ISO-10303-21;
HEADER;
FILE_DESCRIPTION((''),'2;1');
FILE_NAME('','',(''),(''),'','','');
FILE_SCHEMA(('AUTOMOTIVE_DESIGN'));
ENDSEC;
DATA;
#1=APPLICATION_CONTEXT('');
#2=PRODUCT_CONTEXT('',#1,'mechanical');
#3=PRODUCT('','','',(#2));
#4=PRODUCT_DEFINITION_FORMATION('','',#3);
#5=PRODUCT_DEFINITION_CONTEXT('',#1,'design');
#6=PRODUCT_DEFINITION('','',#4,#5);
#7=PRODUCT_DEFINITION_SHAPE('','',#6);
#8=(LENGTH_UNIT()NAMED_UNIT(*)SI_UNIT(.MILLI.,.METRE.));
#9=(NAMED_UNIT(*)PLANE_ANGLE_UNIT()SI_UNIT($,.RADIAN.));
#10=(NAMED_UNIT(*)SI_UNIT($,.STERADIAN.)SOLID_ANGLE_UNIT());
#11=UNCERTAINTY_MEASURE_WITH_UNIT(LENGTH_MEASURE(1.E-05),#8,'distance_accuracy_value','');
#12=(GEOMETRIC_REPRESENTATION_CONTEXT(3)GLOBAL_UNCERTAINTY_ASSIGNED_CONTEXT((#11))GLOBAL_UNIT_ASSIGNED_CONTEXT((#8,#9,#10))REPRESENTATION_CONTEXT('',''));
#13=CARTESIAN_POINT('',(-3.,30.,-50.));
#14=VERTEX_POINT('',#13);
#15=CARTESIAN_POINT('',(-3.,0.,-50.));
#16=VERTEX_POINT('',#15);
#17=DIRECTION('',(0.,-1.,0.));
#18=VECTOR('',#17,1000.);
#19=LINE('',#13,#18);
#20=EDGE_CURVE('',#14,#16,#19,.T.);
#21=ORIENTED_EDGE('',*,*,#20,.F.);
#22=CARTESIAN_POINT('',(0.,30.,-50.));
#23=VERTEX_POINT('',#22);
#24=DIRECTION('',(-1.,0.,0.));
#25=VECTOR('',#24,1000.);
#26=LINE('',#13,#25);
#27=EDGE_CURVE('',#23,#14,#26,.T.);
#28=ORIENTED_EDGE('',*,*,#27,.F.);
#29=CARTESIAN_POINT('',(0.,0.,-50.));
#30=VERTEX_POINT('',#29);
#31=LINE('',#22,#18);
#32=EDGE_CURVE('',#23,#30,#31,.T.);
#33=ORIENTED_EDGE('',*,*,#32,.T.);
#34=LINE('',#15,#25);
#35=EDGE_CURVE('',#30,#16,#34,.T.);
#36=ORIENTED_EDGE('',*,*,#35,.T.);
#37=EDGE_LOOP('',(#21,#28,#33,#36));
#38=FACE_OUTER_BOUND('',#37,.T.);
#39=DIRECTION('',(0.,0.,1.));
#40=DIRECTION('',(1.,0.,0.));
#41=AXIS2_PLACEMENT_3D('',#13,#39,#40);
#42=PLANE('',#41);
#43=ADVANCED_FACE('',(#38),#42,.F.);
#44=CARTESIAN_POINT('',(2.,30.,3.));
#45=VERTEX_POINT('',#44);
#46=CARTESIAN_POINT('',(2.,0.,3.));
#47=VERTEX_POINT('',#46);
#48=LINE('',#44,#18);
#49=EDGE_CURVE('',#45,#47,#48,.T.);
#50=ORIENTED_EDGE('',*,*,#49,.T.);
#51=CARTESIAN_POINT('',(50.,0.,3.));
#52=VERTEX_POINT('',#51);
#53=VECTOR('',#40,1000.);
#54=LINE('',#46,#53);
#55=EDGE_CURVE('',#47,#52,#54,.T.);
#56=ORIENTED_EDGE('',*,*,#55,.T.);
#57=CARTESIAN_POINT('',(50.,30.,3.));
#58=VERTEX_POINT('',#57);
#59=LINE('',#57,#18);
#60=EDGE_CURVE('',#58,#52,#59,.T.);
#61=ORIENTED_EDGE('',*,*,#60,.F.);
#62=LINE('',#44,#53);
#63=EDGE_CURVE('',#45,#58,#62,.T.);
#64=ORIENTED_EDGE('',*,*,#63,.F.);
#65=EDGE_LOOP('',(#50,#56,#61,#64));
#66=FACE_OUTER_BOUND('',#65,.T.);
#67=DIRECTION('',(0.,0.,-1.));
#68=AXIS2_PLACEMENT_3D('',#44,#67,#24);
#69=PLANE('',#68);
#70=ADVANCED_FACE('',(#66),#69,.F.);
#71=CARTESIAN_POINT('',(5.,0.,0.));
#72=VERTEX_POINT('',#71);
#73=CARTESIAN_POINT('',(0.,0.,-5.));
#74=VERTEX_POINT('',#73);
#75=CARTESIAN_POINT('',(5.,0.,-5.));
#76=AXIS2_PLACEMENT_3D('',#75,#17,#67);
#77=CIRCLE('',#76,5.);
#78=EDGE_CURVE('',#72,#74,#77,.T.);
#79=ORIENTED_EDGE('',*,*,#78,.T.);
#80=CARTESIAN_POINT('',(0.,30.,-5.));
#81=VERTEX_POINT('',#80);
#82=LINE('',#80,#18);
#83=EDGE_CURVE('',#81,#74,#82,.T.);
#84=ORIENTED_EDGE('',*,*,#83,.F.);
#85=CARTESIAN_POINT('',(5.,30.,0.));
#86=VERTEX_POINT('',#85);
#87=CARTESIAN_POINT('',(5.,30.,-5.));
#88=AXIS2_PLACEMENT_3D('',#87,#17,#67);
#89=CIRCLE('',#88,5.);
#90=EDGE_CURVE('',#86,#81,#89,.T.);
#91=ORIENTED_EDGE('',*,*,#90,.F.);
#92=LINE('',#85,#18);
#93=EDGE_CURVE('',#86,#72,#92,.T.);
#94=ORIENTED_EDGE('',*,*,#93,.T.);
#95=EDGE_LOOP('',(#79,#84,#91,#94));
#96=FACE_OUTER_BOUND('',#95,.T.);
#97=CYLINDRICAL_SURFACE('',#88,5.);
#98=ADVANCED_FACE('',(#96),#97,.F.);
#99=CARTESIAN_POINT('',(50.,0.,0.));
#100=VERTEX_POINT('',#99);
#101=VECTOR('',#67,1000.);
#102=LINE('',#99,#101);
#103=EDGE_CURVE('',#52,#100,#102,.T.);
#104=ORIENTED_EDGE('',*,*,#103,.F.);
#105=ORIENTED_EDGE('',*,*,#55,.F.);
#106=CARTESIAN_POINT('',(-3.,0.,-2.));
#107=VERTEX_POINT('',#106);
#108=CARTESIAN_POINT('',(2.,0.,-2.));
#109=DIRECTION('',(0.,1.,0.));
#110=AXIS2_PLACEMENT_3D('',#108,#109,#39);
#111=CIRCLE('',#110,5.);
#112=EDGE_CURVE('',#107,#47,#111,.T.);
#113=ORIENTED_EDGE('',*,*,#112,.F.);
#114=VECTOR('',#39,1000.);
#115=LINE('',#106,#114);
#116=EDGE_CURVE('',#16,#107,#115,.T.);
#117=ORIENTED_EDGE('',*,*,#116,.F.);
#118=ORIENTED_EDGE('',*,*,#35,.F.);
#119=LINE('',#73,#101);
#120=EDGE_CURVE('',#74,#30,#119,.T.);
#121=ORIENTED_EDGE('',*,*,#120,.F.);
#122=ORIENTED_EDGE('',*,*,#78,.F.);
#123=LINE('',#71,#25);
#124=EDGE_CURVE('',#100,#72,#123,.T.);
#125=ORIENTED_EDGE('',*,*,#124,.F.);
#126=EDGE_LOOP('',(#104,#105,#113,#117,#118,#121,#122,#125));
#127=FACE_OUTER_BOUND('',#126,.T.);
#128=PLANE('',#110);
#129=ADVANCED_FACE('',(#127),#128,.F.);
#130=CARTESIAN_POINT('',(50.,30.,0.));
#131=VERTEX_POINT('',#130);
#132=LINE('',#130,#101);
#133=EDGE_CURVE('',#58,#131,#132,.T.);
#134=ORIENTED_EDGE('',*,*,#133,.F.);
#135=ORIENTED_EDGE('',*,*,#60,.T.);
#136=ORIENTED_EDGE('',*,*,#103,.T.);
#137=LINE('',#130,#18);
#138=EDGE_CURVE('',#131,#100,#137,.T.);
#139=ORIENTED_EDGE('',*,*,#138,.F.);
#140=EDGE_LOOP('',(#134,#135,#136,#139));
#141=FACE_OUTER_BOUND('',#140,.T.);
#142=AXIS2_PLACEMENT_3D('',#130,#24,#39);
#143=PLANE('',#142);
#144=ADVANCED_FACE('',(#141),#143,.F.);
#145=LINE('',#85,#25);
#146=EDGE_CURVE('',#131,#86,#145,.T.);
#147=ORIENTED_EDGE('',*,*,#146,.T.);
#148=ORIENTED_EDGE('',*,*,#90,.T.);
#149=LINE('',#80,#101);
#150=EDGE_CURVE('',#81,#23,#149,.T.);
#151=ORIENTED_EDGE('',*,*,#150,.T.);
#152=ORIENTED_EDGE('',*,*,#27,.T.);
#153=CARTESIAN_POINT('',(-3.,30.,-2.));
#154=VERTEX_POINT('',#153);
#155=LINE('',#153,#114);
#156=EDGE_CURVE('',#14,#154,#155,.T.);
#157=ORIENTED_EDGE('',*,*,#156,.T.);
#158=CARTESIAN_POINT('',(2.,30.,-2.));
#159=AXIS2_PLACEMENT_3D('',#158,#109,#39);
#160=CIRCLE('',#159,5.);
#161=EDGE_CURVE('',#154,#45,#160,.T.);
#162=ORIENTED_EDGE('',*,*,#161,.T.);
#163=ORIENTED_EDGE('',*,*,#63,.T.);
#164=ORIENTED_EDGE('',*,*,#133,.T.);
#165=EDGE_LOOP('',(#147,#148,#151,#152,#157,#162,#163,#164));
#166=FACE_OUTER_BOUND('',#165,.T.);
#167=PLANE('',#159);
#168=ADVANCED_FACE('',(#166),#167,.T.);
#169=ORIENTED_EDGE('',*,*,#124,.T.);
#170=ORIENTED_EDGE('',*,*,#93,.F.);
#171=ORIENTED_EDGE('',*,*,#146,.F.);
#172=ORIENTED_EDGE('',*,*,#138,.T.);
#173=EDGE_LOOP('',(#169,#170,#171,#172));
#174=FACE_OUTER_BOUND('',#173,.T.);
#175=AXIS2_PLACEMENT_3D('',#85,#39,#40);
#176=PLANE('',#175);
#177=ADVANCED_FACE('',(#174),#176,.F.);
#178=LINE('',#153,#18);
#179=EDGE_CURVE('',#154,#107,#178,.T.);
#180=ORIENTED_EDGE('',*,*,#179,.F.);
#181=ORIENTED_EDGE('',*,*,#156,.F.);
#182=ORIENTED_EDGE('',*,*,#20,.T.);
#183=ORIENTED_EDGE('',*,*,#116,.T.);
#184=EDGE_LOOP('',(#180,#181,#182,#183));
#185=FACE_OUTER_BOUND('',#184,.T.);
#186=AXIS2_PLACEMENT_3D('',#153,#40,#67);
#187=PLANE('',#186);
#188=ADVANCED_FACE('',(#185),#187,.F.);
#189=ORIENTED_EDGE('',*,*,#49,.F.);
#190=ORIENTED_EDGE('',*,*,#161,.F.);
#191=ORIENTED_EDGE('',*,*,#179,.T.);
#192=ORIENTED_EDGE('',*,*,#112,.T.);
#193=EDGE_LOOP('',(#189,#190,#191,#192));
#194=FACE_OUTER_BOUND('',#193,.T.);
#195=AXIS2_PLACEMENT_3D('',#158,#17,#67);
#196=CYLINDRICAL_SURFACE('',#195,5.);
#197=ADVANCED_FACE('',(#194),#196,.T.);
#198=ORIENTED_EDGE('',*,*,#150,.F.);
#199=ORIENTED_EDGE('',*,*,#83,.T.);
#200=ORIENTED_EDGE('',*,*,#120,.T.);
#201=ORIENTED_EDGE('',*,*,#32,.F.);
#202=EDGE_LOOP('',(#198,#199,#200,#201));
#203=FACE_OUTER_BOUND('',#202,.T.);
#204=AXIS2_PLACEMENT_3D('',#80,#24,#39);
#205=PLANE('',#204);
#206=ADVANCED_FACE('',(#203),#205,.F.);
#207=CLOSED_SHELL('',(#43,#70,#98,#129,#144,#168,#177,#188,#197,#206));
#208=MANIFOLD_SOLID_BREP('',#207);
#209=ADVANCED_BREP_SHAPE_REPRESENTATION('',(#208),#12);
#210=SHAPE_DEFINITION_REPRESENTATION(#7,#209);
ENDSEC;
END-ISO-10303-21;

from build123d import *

# Parameters (mm, degrees)
BOSS_EXTRUDE1_DEPTH = 30


with BuildPart() as part:
    # Sketch1 → Boss-Extrude1 (new body)
    with BuildSketch(Plane(origin=(0, 0, 0), x_dir=(1, 0, 0), z_dir=(0, 1, 0))):
        with BuildLine():
            Line((5, 0), (50, 0))
            Line((50, 0), (50, -3))
            Line((50, -3), (2, -3))
            ThreePointArc((2, -3), (-1.535533906, -1.535533906), (-3, 2))
            Line((-3, 2), (-3, 50))
            Line((-3, 50), (0, 50))
            Line((0, 50), (0, 5))
            ThreePointArc((0, 5), (1.464466094, 1.464466094), (5, 0))
        make_face()
    extrude(amount=BOSS_EXTRUDE1_DEPTH)


solid = part.part
